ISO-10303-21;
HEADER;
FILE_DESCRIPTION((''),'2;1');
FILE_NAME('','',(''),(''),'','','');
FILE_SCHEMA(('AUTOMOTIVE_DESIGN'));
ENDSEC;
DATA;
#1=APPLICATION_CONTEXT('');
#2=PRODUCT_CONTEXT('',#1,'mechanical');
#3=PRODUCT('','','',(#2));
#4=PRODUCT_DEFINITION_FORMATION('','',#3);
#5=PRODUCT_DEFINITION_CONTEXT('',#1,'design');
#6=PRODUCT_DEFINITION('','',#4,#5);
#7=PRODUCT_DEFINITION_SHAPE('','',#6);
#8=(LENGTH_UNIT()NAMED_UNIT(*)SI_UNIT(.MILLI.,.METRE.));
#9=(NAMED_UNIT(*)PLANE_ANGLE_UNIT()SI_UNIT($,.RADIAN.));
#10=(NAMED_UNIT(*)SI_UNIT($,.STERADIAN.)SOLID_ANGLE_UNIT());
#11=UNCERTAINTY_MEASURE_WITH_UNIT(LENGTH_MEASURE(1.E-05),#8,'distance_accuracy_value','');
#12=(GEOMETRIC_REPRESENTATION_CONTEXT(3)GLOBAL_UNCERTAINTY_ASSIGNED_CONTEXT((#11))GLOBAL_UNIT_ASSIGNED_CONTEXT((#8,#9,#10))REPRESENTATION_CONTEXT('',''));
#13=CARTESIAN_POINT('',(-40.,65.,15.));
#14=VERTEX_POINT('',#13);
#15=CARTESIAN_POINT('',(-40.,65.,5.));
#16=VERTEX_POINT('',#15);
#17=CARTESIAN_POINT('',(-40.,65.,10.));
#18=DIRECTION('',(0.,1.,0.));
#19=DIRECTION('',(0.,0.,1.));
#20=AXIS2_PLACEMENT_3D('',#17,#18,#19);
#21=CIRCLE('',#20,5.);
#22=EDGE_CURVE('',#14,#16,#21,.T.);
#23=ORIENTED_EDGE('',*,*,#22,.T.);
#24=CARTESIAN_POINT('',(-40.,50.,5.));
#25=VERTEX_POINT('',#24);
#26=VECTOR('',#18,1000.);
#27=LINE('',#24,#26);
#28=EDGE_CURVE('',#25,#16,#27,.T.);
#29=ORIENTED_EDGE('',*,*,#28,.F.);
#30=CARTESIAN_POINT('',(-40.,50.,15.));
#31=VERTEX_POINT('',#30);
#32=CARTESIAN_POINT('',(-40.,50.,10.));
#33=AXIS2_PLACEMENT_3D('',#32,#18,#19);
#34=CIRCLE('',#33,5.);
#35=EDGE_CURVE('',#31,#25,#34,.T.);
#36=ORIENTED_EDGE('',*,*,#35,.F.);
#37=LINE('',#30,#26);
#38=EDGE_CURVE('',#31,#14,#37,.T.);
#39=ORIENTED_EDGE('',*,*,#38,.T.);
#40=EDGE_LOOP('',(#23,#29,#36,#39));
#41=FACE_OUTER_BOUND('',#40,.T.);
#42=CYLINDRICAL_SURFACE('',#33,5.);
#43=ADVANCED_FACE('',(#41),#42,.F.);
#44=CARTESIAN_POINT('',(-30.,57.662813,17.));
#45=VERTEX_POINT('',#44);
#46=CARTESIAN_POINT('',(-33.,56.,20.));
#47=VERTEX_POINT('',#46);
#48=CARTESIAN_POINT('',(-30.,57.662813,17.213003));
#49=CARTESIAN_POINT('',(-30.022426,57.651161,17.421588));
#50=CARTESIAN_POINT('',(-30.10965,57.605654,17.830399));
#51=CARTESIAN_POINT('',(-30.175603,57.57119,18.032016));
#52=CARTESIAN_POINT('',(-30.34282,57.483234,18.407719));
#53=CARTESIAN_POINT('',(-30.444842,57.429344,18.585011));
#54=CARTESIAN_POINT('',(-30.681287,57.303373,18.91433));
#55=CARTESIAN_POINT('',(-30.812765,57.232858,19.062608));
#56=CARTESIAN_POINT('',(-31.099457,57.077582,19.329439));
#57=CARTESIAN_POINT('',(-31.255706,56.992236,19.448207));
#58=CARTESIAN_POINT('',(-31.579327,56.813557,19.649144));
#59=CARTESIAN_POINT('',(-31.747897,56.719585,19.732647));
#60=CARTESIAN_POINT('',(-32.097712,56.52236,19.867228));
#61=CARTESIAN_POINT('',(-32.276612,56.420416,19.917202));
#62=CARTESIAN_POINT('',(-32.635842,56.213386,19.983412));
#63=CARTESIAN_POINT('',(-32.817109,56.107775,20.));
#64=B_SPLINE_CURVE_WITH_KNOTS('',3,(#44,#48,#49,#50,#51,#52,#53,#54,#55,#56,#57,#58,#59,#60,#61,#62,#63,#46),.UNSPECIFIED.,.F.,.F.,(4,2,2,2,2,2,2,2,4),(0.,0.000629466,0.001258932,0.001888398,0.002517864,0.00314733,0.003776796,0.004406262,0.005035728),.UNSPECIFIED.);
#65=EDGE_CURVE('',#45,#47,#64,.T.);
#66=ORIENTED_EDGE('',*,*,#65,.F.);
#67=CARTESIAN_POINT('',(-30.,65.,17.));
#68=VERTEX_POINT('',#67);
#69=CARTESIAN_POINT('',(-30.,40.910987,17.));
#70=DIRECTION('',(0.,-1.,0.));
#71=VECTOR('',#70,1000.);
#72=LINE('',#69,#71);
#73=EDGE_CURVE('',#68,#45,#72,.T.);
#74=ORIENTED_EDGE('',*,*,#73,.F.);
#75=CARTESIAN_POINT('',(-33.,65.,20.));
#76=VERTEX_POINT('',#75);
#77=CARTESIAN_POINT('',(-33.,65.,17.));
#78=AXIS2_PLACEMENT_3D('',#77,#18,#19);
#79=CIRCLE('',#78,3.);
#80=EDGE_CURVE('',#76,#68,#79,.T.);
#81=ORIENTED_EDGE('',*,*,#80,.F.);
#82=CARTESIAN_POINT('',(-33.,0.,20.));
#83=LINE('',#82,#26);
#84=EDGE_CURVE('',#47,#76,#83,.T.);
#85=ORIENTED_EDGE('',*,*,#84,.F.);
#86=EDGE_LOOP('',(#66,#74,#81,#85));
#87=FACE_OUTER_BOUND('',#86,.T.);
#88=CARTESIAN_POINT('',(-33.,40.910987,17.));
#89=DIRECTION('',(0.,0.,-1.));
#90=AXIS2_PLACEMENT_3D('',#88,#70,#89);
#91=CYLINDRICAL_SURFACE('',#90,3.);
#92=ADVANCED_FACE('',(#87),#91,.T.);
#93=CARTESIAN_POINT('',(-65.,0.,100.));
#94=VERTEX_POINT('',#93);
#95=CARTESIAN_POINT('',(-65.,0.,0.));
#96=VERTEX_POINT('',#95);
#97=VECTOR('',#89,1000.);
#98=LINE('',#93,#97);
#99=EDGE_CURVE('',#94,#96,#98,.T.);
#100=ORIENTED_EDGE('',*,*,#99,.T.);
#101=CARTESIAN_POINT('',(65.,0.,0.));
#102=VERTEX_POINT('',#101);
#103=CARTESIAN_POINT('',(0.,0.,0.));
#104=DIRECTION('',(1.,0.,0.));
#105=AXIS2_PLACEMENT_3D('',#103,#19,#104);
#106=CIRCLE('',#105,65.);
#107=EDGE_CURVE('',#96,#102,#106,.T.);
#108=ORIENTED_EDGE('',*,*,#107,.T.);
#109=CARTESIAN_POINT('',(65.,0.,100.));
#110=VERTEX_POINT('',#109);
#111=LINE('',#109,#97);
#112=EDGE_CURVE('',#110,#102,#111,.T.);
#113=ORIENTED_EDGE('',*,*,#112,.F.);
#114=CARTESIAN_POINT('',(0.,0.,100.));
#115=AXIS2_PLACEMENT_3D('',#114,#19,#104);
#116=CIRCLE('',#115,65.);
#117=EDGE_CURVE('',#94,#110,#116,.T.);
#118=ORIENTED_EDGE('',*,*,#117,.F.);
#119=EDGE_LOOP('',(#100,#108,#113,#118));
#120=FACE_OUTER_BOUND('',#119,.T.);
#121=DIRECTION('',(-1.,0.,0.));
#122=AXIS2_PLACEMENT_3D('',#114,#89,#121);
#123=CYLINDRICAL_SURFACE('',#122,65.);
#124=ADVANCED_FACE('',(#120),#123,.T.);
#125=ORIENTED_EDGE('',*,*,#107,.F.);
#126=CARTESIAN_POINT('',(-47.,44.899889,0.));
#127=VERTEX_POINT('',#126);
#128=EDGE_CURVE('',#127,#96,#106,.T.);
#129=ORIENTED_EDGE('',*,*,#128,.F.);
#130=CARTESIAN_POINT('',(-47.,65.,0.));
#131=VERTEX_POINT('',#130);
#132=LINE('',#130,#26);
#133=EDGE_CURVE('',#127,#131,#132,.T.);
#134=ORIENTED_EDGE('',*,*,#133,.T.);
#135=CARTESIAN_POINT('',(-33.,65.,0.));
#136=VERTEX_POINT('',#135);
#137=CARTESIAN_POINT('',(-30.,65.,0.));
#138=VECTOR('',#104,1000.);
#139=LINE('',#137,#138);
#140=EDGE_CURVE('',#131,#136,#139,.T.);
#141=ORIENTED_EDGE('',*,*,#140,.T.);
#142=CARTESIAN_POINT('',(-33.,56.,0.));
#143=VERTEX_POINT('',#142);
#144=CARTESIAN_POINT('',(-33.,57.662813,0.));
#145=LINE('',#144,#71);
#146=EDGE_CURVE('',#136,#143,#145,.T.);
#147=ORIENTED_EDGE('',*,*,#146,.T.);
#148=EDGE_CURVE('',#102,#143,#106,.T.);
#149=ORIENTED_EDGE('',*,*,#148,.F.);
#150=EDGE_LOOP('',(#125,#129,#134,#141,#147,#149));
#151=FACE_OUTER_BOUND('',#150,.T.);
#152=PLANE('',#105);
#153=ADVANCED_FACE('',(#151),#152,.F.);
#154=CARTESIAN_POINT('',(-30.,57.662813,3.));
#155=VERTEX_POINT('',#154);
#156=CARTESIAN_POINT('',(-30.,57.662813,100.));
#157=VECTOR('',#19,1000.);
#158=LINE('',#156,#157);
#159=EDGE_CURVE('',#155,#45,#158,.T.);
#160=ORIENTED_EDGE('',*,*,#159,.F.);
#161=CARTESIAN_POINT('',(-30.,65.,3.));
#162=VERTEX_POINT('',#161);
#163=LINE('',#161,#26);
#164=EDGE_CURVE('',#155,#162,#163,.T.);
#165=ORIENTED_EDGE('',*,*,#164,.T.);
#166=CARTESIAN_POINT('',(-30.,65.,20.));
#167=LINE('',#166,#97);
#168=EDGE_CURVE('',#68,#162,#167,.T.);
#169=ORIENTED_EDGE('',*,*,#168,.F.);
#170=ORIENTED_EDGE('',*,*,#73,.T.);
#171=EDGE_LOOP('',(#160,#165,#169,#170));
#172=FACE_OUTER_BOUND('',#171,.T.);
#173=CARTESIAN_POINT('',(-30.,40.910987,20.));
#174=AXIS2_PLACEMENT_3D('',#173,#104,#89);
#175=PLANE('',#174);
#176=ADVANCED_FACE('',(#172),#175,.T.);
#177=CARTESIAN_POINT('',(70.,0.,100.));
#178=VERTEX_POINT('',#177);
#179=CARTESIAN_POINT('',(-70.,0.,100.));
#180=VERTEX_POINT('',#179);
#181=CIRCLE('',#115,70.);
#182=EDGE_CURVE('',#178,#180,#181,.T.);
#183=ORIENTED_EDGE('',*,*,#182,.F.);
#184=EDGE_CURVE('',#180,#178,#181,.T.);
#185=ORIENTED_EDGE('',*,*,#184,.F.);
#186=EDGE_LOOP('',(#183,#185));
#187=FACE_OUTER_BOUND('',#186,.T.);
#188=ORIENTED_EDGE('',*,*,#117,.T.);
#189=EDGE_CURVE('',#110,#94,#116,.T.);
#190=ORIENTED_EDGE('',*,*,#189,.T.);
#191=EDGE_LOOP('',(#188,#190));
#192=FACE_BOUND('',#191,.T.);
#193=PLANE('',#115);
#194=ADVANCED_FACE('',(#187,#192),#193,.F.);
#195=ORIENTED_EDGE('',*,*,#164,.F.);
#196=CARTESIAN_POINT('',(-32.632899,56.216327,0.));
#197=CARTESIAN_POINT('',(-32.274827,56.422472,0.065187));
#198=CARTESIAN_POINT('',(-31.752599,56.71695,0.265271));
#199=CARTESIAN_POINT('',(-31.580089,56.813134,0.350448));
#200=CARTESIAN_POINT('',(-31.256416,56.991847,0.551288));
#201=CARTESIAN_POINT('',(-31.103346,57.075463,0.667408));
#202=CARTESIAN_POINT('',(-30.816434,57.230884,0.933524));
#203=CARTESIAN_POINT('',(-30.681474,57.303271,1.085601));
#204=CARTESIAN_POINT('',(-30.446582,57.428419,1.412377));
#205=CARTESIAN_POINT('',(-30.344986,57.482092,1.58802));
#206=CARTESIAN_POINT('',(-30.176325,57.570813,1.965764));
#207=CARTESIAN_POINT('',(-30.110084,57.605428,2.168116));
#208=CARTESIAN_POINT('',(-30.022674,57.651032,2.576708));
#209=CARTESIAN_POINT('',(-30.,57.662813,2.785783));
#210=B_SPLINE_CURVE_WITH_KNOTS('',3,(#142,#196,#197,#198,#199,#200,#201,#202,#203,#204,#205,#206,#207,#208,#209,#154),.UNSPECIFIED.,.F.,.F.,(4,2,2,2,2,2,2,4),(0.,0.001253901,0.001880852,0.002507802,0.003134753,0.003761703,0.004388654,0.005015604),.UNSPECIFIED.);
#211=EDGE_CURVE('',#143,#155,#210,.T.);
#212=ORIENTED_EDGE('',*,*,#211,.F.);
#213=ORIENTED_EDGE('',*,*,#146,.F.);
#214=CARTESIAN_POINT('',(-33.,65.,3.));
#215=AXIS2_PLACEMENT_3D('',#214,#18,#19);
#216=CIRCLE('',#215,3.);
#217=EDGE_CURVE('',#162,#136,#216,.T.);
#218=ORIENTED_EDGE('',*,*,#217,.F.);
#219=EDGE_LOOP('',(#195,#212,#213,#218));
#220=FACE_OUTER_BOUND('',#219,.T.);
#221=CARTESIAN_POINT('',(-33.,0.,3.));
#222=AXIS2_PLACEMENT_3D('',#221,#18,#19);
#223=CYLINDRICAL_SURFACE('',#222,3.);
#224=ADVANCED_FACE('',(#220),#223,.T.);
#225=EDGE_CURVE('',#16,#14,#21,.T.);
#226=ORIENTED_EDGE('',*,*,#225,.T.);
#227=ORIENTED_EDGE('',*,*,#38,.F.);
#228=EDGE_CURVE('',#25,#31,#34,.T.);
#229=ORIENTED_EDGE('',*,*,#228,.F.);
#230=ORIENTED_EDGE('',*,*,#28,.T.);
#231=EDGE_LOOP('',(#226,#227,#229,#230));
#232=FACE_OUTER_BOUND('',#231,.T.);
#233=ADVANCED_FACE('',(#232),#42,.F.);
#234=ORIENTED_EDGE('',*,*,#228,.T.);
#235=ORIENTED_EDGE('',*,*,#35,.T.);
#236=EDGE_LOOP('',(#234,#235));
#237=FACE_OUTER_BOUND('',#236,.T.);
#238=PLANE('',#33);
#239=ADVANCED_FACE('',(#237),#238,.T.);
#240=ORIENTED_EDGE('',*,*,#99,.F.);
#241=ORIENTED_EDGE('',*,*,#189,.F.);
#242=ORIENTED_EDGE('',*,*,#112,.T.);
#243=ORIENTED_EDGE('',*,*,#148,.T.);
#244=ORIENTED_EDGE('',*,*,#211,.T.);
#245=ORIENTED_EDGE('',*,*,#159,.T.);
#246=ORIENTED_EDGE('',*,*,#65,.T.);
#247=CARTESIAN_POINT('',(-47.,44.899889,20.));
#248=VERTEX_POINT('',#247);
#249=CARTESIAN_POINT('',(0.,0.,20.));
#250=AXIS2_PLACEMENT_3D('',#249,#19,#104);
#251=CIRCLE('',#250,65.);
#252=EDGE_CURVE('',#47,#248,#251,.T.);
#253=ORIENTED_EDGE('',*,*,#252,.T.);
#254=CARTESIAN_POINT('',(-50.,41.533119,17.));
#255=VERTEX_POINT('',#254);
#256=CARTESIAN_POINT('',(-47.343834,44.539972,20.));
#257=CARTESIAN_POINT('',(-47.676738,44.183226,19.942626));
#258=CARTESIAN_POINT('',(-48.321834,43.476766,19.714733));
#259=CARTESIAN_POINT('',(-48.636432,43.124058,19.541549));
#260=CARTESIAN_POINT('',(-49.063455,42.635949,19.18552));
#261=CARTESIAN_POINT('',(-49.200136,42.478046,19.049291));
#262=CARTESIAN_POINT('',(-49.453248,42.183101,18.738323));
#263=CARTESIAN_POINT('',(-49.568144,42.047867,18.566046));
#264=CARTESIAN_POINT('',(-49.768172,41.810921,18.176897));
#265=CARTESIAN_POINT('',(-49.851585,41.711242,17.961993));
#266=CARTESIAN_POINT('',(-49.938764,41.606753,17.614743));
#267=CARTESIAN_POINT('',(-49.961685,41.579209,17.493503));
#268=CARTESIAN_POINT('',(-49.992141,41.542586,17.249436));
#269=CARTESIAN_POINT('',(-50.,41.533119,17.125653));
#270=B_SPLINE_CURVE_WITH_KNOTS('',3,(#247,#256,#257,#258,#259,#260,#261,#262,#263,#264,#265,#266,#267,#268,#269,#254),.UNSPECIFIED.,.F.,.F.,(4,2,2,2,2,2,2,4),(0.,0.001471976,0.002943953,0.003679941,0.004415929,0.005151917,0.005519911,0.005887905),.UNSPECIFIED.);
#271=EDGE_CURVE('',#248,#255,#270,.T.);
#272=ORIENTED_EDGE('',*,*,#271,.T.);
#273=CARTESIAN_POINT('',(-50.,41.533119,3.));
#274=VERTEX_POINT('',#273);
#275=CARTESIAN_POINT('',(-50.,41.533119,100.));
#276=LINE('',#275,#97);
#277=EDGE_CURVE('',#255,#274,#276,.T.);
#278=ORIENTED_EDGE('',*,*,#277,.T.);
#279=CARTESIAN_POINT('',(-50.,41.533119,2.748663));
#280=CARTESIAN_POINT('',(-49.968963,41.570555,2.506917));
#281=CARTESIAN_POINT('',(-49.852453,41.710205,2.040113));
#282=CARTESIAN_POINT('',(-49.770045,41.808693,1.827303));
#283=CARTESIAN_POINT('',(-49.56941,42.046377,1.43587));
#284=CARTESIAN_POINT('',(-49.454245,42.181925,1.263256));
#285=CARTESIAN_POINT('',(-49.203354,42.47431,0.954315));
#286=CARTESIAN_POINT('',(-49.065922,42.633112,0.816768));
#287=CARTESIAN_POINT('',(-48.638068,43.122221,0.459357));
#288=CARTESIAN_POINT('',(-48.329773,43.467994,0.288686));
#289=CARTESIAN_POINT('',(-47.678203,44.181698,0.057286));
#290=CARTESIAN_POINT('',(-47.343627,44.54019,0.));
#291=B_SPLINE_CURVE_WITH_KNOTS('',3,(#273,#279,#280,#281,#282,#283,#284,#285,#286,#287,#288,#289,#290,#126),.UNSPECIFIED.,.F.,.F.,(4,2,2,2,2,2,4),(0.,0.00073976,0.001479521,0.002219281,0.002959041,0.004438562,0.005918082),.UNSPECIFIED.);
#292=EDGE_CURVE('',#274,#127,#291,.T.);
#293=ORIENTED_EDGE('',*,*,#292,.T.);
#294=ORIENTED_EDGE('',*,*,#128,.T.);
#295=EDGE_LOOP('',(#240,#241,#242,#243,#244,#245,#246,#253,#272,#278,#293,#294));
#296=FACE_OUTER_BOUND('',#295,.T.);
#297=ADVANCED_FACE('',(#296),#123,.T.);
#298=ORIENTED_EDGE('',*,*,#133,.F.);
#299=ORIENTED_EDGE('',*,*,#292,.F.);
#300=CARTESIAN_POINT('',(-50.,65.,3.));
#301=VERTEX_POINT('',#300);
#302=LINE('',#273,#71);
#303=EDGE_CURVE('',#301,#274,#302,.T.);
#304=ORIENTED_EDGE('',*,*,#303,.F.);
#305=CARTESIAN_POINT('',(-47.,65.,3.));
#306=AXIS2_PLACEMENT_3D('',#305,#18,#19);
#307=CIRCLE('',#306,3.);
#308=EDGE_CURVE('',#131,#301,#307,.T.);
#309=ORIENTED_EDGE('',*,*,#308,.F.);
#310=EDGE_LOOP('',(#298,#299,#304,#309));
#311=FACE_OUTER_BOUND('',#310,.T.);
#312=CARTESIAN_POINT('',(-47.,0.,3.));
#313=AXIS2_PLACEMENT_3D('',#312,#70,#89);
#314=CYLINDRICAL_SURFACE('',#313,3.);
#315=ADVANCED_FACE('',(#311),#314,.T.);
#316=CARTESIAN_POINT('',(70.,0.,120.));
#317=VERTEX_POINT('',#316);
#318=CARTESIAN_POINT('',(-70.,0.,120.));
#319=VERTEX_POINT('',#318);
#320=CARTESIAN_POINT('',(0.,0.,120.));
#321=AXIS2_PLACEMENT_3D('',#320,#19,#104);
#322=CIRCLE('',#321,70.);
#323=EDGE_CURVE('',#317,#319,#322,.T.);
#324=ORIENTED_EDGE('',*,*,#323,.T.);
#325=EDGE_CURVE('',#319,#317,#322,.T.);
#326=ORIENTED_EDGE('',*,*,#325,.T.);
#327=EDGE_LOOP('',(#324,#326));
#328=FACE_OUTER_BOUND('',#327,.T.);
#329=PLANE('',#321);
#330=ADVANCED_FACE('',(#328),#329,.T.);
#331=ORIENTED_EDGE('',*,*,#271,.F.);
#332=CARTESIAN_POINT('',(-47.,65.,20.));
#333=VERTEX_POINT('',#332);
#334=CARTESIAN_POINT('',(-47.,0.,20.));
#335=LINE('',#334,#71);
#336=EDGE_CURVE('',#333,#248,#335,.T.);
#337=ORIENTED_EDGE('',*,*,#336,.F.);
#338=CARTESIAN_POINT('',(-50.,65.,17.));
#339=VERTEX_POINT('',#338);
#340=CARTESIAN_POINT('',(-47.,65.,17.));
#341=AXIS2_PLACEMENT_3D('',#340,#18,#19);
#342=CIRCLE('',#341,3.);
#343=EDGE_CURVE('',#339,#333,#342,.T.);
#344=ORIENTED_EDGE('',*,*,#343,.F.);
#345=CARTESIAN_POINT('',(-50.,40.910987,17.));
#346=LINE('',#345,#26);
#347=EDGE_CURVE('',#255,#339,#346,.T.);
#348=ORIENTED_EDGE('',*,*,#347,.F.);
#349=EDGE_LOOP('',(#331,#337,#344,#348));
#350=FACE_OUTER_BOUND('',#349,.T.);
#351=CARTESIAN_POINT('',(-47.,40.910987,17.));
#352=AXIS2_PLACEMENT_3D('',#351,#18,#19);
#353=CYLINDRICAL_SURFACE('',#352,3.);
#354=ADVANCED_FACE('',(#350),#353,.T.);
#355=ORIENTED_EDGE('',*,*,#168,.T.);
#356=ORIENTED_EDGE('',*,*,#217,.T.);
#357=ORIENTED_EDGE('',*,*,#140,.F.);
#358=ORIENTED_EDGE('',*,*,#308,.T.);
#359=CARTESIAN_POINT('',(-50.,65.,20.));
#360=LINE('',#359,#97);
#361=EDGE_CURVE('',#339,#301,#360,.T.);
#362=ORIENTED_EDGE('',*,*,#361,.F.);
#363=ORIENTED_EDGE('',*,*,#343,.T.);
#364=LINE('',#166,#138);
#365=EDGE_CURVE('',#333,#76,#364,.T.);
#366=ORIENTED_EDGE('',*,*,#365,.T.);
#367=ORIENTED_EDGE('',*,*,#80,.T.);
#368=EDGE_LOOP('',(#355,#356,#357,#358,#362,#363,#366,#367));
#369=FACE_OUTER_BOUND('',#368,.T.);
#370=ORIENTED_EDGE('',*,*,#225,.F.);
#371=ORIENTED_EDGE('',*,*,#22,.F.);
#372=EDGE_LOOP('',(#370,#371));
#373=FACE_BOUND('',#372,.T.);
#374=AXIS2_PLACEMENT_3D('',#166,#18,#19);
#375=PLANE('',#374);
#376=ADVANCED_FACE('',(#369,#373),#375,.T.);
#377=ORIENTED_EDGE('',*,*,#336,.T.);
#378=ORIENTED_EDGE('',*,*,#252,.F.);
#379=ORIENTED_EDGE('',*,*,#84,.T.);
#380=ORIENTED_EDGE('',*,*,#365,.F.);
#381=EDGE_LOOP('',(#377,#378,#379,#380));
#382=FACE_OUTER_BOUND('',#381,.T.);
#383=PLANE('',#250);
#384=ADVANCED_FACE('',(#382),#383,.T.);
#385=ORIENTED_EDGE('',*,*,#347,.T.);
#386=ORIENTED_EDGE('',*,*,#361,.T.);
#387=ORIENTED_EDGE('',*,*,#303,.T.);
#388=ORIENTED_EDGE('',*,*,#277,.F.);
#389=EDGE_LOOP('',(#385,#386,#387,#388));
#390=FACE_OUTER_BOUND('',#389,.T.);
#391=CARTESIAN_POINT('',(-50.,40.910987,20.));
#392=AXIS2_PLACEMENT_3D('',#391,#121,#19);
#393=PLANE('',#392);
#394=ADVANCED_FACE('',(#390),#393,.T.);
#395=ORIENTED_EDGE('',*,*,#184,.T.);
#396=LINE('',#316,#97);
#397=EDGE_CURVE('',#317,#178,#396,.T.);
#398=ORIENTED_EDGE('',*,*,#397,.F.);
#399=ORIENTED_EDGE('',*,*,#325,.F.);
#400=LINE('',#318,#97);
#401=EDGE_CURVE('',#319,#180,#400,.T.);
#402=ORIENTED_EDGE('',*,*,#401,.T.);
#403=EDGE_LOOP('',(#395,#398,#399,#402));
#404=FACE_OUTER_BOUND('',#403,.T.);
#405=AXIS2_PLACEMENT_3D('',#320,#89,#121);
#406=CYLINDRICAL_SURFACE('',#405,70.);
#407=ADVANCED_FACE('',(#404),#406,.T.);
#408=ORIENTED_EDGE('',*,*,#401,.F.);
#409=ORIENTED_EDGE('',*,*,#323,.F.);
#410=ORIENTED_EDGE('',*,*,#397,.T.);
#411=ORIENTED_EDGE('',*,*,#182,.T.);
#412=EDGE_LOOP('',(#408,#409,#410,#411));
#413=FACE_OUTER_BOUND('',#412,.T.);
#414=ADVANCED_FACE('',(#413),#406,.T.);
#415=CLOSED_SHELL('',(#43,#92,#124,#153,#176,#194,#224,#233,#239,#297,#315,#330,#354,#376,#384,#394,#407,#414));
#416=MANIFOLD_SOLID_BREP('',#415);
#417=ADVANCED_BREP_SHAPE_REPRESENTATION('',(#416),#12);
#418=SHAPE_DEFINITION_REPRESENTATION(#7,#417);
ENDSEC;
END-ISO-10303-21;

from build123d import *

# Parameters (mm, degrees)
SKETCH1_R           = 65
BOSS_EXTRUDE1_DEPTH = 100
SKETCH2_R           = 70
BOSS_EXTRUDE2_DEPTH = 20
SKETCH4_W           = 20
SKETCH4_H           = 24.089012679
BOSS_EXTRUDE4_DEPTH = 20
SKETCH5_R           = 5
CUT_EXTRUDE1_DEPTH  = 15
FILLET1_R           = 3


with BuildPart() as part:
    # Sketch1 → Boss-Extrude1 (new body)
    with BuildSketch(Plane.XY):
        Circle(SKETCH1_R)
    extrude(amount=BOSS_EXTRUDE1_DEPTH)

    # Sketch2 → Boss-Extrude2 (add)
    with BuildSketch(Plane.XY.offset(100)):
        Circle(SKETCH2_R)
    extrude(amount=BOSS_EXTRUDE2_DEPTH)

    # Sketch4 → Boss-Extrude4 (add)
    with BuildSketch(Plane(origin=(0, 0, 0), x_dir=(-1, 0, 0), z_dir=(0, 0, -1))):
        with Locations((40, 52.95549366)):
            Rectangle(SKETCH4_W, SKETCH4_H)
    extrude(amount=-BOSS_EXTRUDE4_DEPTH)

    # Sketch5 → Cut-Extrude1 (cut)
    with BuildSketch(Plane(origin=(0, 65, 0), x_dir=(1, 0, 0), z_dir=(0, 1, 0))):
        with Locations(Location((-40, -10, 0), (0, 0, 270))):
            Circle(SKETCH5_R)
    extrude(amount=-CUT_EXTRUDE1_DEPTH, mode=Mode.SUBTRACT)

    # Fillet1
    fillet1_edges = [part.edges().sort_by_distance(p)[0] for p in [
        (-30, 61.331406487, 20),
        (-50, 53.266559657, 20),
        (-30, 61.331406487, 0),
        (-50, 53.266559657, 0),
    ]]
    fillet(fillet1_edges, radius=FILLET1_R)


solid = part.part
